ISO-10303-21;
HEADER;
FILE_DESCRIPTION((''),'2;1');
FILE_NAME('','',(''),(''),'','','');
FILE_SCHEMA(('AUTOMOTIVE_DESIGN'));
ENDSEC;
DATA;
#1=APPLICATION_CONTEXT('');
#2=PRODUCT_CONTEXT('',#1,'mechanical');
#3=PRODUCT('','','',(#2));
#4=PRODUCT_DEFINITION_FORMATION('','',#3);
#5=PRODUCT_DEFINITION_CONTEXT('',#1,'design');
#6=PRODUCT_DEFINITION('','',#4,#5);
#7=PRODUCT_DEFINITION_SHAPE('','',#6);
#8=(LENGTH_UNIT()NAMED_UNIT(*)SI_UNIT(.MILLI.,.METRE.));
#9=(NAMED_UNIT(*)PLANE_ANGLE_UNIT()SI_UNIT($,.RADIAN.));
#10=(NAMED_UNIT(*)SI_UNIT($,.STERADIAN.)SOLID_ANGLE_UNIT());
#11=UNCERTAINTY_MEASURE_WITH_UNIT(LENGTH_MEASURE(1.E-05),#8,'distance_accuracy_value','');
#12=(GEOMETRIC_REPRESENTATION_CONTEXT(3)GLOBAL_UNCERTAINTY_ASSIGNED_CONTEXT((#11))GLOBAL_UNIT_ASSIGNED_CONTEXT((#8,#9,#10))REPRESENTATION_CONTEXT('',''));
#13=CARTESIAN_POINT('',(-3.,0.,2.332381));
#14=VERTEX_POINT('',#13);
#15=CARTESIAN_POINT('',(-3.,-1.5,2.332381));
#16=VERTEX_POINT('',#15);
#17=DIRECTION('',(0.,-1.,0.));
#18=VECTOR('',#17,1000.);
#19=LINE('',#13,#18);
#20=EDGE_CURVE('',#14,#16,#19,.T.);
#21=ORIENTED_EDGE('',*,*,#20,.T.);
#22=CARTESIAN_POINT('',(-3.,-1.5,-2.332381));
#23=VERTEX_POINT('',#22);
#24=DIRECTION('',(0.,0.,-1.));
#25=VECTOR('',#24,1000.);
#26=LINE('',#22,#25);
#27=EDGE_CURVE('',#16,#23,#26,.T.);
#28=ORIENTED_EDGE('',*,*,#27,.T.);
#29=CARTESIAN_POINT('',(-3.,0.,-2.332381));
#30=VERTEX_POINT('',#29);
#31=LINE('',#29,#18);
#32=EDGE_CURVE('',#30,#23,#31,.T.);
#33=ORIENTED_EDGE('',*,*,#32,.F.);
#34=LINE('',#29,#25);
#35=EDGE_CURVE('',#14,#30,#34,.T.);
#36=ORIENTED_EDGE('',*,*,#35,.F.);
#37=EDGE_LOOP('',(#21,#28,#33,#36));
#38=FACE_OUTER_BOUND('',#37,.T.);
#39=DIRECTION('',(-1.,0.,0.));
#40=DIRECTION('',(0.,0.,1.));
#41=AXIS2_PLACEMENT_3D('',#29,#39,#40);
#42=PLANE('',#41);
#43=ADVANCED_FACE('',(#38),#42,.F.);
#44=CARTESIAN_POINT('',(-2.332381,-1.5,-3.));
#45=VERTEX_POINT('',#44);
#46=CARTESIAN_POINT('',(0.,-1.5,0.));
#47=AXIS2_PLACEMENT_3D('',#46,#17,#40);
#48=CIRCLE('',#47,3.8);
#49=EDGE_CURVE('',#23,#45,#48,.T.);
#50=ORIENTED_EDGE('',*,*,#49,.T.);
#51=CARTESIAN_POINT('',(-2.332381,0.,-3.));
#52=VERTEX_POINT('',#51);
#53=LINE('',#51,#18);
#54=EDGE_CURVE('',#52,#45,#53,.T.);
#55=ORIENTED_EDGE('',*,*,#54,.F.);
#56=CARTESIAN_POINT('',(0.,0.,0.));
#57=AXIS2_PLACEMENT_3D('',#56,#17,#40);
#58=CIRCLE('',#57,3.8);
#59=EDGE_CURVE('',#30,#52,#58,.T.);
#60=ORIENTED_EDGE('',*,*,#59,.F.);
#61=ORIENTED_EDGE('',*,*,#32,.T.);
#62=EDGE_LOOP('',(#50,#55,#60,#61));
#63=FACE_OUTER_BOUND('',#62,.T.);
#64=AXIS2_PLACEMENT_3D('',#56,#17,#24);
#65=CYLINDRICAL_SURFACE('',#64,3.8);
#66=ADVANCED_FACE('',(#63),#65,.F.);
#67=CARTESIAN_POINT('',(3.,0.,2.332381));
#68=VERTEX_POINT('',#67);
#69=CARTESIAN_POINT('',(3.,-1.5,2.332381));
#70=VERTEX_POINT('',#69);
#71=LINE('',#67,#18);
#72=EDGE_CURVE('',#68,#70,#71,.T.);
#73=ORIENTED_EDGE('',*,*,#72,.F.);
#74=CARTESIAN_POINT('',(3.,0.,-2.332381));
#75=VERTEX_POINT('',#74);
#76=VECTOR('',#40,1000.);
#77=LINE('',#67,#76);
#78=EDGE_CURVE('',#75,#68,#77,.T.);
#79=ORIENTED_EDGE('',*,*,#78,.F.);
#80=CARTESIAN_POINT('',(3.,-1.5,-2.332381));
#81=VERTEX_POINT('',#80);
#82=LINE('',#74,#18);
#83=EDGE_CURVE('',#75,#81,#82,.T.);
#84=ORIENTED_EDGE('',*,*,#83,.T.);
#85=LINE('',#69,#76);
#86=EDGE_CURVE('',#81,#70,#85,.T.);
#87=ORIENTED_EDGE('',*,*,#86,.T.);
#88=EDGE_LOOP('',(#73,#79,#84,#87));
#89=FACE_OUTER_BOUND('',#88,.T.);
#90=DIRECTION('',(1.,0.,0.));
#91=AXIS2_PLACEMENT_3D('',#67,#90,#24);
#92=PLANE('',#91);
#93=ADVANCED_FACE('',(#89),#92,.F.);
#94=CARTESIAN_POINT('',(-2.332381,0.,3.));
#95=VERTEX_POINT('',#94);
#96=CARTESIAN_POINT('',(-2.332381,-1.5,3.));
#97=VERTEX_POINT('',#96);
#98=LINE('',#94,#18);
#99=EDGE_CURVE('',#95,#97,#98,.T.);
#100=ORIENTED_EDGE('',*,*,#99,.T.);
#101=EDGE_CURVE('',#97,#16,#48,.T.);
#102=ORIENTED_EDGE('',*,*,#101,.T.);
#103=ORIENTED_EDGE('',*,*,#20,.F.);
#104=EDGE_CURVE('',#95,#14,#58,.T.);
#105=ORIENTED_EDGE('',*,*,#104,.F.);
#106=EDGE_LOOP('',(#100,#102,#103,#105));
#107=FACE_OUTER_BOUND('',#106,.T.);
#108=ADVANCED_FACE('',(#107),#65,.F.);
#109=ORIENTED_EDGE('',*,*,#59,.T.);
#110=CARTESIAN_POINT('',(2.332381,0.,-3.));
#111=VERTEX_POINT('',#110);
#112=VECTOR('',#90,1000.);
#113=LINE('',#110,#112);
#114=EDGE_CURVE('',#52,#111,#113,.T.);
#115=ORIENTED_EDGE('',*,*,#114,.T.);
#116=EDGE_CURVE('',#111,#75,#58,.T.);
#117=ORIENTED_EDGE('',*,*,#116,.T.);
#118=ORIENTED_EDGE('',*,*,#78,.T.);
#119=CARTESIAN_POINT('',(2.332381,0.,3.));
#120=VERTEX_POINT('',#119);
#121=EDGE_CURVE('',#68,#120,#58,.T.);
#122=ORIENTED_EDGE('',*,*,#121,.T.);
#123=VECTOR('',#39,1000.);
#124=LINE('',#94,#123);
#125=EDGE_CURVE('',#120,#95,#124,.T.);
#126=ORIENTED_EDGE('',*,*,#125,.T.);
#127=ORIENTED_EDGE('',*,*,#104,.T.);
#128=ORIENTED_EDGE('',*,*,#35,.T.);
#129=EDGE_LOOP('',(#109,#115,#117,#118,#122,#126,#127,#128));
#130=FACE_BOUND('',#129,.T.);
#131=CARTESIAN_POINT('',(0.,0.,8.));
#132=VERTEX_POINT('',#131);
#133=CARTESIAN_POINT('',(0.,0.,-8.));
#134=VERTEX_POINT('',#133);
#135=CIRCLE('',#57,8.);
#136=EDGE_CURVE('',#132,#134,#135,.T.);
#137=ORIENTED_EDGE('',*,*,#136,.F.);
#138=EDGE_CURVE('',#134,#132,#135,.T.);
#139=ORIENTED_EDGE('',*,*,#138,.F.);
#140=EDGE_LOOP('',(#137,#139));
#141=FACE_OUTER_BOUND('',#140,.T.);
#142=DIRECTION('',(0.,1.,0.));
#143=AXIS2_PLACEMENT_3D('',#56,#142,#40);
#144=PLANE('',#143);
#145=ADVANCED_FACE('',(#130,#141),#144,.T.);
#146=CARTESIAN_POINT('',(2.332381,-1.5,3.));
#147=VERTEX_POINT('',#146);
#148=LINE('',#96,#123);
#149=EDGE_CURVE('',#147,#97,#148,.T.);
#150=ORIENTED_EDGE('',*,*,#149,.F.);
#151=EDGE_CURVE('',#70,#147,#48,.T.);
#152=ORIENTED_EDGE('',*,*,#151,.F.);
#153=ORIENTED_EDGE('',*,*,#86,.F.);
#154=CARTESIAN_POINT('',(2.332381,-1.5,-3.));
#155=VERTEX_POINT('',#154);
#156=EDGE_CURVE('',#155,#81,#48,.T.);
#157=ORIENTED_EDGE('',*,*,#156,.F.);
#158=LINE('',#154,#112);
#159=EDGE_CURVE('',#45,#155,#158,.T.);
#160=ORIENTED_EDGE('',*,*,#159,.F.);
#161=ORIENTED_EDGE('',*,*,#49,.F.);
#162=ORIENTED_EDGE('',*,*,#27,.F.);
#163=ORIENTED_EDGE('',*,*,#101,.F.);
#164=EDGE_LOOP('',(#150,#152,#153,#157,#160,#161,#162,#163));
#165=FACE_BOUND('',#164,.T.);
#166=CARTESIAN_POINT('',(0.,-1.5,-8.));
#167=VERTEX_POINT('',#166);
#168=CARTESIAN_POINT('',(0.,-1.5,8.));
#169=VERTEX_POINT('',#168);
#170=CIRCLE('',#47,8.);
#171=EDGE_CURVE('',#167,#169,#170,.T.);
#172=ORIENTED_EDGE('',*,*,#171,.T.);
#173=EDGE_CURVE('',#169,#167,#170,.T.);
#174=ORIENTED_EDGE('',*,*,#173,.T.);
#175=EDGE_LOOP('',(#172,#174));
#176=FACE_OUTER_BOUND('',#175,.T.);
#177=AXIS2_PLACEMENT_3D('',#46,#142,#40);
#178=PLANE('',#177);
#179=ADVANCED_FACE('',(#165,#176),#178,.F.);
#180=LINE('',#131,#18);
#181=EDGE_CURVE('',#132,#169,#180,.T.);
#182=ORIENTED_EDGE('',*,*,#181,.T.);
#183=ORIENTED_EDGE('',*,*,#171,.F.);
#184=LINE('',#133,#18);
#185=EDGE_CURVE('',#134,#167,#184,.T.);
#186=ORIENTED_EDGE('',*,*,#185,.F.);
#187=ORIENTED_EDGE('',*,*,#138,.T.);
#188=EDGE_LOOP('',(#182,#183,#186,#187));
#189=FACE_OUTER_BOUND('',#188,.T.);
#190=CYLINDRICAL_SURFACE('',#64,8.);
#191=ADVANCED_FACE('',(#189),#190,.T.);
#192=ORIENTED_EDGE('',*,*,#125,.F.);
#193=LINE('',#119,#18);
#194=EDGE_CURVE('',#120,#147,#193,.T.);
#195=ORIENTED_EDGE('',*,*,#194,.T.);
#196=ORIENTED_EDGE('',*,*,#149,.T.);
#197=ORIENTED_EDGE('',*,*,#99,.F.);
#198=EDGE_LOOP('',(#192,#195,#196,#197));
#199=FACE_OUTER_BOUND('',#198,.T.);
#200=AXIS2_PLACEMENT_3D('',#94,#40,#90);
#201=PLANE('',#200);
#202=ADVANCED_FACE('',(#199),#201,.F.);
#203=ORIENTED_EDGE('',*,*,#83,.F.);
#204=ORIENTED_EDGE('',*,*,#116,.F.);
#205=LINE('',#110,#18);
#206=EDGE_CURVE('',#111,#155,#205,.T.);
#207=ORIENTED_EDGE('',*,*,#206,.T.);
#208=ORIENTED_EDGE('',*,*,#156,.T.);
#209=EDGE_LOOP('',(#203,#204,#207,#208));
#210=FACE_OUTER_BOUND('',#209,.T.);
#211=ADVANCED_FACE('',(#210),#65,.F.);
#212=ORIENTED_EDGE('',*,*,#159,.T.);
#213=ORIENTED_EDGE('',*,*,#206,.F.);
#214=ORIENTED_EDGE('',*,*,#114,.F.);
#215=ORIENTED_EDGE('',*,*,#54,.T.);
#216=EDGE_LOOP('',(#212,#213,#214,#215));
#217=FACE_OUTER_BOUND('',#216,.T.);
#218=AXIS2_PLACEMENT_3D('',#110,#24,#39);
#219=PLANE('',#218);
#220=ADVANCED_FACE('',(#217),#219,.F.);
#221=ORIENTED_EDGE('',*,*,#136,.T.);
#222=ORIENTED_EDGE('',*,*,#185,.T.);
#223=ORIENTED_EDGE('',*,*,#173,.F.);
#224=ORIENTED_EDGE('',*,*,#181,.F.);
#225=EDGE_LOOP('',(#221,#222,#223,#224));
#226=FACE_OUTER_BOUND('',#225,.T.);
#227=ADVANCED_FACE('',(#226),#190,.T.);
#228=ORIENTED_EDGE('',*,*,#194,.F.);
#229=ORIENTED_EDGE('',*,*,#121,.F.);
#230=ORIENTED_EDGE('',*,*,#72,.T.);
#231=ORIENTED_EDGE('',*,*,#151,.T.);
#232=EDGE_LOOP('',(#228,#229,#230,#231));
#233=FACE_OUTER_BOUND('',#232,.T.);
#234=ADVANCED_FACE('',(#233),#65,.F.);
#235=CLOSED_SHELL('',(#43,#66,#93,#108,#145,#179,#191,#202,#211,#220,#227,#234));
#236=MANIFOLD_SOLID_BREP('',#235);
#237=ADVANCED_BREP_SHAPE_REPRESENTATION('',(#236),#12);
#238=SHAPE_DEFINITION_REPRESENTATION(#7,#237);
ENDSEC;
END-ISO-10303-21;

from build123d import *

# Parameters (mm, degrees)
SKETCH1_R           = 8
BOSS_EXTRUDE1_DEPTH = 1.5


with BuildPart() as part:
    # Sketch1 → Boss-Extrude1 (new body)
    with BuildSketch(Plane.XZ.offset(1.5)):
        with Locations(Location((0, 0, 0), (0, 0, 90))):
            Circle(SKETCH1_R)
        with BuildLine():
            Line((3, 2.332380758), (3, -2.332380758))
            ThreePointArc((3, -2.332380758), (2.687005769, -2.687005769), (2.332380758, -3))
            Line((2.332380758, -3), (-2.332380758, -3))
            ThreePointArc((-2.332380758, -3), (-2.687005769, -2.687005769), (-3, -2.332380758))
            Line((-3, -2.332380758), (-3, 2.332380758))
            ThreePointArc((-3, 2.332380758), (-2.687005769, 2.687005769), (-2.332380758, 3))
            Line((-2.332380758, 3), (2.332380758, 3))
            ThreePointArc((2.332380758, 3), (2.687005769, 2.687005769), (3, 2.332380758))
        make_face(mode=Mode.SUBTRACT)
    extrude(amount=-BOSS_EXTRUDE1_DEPTH)


solid = part.part
